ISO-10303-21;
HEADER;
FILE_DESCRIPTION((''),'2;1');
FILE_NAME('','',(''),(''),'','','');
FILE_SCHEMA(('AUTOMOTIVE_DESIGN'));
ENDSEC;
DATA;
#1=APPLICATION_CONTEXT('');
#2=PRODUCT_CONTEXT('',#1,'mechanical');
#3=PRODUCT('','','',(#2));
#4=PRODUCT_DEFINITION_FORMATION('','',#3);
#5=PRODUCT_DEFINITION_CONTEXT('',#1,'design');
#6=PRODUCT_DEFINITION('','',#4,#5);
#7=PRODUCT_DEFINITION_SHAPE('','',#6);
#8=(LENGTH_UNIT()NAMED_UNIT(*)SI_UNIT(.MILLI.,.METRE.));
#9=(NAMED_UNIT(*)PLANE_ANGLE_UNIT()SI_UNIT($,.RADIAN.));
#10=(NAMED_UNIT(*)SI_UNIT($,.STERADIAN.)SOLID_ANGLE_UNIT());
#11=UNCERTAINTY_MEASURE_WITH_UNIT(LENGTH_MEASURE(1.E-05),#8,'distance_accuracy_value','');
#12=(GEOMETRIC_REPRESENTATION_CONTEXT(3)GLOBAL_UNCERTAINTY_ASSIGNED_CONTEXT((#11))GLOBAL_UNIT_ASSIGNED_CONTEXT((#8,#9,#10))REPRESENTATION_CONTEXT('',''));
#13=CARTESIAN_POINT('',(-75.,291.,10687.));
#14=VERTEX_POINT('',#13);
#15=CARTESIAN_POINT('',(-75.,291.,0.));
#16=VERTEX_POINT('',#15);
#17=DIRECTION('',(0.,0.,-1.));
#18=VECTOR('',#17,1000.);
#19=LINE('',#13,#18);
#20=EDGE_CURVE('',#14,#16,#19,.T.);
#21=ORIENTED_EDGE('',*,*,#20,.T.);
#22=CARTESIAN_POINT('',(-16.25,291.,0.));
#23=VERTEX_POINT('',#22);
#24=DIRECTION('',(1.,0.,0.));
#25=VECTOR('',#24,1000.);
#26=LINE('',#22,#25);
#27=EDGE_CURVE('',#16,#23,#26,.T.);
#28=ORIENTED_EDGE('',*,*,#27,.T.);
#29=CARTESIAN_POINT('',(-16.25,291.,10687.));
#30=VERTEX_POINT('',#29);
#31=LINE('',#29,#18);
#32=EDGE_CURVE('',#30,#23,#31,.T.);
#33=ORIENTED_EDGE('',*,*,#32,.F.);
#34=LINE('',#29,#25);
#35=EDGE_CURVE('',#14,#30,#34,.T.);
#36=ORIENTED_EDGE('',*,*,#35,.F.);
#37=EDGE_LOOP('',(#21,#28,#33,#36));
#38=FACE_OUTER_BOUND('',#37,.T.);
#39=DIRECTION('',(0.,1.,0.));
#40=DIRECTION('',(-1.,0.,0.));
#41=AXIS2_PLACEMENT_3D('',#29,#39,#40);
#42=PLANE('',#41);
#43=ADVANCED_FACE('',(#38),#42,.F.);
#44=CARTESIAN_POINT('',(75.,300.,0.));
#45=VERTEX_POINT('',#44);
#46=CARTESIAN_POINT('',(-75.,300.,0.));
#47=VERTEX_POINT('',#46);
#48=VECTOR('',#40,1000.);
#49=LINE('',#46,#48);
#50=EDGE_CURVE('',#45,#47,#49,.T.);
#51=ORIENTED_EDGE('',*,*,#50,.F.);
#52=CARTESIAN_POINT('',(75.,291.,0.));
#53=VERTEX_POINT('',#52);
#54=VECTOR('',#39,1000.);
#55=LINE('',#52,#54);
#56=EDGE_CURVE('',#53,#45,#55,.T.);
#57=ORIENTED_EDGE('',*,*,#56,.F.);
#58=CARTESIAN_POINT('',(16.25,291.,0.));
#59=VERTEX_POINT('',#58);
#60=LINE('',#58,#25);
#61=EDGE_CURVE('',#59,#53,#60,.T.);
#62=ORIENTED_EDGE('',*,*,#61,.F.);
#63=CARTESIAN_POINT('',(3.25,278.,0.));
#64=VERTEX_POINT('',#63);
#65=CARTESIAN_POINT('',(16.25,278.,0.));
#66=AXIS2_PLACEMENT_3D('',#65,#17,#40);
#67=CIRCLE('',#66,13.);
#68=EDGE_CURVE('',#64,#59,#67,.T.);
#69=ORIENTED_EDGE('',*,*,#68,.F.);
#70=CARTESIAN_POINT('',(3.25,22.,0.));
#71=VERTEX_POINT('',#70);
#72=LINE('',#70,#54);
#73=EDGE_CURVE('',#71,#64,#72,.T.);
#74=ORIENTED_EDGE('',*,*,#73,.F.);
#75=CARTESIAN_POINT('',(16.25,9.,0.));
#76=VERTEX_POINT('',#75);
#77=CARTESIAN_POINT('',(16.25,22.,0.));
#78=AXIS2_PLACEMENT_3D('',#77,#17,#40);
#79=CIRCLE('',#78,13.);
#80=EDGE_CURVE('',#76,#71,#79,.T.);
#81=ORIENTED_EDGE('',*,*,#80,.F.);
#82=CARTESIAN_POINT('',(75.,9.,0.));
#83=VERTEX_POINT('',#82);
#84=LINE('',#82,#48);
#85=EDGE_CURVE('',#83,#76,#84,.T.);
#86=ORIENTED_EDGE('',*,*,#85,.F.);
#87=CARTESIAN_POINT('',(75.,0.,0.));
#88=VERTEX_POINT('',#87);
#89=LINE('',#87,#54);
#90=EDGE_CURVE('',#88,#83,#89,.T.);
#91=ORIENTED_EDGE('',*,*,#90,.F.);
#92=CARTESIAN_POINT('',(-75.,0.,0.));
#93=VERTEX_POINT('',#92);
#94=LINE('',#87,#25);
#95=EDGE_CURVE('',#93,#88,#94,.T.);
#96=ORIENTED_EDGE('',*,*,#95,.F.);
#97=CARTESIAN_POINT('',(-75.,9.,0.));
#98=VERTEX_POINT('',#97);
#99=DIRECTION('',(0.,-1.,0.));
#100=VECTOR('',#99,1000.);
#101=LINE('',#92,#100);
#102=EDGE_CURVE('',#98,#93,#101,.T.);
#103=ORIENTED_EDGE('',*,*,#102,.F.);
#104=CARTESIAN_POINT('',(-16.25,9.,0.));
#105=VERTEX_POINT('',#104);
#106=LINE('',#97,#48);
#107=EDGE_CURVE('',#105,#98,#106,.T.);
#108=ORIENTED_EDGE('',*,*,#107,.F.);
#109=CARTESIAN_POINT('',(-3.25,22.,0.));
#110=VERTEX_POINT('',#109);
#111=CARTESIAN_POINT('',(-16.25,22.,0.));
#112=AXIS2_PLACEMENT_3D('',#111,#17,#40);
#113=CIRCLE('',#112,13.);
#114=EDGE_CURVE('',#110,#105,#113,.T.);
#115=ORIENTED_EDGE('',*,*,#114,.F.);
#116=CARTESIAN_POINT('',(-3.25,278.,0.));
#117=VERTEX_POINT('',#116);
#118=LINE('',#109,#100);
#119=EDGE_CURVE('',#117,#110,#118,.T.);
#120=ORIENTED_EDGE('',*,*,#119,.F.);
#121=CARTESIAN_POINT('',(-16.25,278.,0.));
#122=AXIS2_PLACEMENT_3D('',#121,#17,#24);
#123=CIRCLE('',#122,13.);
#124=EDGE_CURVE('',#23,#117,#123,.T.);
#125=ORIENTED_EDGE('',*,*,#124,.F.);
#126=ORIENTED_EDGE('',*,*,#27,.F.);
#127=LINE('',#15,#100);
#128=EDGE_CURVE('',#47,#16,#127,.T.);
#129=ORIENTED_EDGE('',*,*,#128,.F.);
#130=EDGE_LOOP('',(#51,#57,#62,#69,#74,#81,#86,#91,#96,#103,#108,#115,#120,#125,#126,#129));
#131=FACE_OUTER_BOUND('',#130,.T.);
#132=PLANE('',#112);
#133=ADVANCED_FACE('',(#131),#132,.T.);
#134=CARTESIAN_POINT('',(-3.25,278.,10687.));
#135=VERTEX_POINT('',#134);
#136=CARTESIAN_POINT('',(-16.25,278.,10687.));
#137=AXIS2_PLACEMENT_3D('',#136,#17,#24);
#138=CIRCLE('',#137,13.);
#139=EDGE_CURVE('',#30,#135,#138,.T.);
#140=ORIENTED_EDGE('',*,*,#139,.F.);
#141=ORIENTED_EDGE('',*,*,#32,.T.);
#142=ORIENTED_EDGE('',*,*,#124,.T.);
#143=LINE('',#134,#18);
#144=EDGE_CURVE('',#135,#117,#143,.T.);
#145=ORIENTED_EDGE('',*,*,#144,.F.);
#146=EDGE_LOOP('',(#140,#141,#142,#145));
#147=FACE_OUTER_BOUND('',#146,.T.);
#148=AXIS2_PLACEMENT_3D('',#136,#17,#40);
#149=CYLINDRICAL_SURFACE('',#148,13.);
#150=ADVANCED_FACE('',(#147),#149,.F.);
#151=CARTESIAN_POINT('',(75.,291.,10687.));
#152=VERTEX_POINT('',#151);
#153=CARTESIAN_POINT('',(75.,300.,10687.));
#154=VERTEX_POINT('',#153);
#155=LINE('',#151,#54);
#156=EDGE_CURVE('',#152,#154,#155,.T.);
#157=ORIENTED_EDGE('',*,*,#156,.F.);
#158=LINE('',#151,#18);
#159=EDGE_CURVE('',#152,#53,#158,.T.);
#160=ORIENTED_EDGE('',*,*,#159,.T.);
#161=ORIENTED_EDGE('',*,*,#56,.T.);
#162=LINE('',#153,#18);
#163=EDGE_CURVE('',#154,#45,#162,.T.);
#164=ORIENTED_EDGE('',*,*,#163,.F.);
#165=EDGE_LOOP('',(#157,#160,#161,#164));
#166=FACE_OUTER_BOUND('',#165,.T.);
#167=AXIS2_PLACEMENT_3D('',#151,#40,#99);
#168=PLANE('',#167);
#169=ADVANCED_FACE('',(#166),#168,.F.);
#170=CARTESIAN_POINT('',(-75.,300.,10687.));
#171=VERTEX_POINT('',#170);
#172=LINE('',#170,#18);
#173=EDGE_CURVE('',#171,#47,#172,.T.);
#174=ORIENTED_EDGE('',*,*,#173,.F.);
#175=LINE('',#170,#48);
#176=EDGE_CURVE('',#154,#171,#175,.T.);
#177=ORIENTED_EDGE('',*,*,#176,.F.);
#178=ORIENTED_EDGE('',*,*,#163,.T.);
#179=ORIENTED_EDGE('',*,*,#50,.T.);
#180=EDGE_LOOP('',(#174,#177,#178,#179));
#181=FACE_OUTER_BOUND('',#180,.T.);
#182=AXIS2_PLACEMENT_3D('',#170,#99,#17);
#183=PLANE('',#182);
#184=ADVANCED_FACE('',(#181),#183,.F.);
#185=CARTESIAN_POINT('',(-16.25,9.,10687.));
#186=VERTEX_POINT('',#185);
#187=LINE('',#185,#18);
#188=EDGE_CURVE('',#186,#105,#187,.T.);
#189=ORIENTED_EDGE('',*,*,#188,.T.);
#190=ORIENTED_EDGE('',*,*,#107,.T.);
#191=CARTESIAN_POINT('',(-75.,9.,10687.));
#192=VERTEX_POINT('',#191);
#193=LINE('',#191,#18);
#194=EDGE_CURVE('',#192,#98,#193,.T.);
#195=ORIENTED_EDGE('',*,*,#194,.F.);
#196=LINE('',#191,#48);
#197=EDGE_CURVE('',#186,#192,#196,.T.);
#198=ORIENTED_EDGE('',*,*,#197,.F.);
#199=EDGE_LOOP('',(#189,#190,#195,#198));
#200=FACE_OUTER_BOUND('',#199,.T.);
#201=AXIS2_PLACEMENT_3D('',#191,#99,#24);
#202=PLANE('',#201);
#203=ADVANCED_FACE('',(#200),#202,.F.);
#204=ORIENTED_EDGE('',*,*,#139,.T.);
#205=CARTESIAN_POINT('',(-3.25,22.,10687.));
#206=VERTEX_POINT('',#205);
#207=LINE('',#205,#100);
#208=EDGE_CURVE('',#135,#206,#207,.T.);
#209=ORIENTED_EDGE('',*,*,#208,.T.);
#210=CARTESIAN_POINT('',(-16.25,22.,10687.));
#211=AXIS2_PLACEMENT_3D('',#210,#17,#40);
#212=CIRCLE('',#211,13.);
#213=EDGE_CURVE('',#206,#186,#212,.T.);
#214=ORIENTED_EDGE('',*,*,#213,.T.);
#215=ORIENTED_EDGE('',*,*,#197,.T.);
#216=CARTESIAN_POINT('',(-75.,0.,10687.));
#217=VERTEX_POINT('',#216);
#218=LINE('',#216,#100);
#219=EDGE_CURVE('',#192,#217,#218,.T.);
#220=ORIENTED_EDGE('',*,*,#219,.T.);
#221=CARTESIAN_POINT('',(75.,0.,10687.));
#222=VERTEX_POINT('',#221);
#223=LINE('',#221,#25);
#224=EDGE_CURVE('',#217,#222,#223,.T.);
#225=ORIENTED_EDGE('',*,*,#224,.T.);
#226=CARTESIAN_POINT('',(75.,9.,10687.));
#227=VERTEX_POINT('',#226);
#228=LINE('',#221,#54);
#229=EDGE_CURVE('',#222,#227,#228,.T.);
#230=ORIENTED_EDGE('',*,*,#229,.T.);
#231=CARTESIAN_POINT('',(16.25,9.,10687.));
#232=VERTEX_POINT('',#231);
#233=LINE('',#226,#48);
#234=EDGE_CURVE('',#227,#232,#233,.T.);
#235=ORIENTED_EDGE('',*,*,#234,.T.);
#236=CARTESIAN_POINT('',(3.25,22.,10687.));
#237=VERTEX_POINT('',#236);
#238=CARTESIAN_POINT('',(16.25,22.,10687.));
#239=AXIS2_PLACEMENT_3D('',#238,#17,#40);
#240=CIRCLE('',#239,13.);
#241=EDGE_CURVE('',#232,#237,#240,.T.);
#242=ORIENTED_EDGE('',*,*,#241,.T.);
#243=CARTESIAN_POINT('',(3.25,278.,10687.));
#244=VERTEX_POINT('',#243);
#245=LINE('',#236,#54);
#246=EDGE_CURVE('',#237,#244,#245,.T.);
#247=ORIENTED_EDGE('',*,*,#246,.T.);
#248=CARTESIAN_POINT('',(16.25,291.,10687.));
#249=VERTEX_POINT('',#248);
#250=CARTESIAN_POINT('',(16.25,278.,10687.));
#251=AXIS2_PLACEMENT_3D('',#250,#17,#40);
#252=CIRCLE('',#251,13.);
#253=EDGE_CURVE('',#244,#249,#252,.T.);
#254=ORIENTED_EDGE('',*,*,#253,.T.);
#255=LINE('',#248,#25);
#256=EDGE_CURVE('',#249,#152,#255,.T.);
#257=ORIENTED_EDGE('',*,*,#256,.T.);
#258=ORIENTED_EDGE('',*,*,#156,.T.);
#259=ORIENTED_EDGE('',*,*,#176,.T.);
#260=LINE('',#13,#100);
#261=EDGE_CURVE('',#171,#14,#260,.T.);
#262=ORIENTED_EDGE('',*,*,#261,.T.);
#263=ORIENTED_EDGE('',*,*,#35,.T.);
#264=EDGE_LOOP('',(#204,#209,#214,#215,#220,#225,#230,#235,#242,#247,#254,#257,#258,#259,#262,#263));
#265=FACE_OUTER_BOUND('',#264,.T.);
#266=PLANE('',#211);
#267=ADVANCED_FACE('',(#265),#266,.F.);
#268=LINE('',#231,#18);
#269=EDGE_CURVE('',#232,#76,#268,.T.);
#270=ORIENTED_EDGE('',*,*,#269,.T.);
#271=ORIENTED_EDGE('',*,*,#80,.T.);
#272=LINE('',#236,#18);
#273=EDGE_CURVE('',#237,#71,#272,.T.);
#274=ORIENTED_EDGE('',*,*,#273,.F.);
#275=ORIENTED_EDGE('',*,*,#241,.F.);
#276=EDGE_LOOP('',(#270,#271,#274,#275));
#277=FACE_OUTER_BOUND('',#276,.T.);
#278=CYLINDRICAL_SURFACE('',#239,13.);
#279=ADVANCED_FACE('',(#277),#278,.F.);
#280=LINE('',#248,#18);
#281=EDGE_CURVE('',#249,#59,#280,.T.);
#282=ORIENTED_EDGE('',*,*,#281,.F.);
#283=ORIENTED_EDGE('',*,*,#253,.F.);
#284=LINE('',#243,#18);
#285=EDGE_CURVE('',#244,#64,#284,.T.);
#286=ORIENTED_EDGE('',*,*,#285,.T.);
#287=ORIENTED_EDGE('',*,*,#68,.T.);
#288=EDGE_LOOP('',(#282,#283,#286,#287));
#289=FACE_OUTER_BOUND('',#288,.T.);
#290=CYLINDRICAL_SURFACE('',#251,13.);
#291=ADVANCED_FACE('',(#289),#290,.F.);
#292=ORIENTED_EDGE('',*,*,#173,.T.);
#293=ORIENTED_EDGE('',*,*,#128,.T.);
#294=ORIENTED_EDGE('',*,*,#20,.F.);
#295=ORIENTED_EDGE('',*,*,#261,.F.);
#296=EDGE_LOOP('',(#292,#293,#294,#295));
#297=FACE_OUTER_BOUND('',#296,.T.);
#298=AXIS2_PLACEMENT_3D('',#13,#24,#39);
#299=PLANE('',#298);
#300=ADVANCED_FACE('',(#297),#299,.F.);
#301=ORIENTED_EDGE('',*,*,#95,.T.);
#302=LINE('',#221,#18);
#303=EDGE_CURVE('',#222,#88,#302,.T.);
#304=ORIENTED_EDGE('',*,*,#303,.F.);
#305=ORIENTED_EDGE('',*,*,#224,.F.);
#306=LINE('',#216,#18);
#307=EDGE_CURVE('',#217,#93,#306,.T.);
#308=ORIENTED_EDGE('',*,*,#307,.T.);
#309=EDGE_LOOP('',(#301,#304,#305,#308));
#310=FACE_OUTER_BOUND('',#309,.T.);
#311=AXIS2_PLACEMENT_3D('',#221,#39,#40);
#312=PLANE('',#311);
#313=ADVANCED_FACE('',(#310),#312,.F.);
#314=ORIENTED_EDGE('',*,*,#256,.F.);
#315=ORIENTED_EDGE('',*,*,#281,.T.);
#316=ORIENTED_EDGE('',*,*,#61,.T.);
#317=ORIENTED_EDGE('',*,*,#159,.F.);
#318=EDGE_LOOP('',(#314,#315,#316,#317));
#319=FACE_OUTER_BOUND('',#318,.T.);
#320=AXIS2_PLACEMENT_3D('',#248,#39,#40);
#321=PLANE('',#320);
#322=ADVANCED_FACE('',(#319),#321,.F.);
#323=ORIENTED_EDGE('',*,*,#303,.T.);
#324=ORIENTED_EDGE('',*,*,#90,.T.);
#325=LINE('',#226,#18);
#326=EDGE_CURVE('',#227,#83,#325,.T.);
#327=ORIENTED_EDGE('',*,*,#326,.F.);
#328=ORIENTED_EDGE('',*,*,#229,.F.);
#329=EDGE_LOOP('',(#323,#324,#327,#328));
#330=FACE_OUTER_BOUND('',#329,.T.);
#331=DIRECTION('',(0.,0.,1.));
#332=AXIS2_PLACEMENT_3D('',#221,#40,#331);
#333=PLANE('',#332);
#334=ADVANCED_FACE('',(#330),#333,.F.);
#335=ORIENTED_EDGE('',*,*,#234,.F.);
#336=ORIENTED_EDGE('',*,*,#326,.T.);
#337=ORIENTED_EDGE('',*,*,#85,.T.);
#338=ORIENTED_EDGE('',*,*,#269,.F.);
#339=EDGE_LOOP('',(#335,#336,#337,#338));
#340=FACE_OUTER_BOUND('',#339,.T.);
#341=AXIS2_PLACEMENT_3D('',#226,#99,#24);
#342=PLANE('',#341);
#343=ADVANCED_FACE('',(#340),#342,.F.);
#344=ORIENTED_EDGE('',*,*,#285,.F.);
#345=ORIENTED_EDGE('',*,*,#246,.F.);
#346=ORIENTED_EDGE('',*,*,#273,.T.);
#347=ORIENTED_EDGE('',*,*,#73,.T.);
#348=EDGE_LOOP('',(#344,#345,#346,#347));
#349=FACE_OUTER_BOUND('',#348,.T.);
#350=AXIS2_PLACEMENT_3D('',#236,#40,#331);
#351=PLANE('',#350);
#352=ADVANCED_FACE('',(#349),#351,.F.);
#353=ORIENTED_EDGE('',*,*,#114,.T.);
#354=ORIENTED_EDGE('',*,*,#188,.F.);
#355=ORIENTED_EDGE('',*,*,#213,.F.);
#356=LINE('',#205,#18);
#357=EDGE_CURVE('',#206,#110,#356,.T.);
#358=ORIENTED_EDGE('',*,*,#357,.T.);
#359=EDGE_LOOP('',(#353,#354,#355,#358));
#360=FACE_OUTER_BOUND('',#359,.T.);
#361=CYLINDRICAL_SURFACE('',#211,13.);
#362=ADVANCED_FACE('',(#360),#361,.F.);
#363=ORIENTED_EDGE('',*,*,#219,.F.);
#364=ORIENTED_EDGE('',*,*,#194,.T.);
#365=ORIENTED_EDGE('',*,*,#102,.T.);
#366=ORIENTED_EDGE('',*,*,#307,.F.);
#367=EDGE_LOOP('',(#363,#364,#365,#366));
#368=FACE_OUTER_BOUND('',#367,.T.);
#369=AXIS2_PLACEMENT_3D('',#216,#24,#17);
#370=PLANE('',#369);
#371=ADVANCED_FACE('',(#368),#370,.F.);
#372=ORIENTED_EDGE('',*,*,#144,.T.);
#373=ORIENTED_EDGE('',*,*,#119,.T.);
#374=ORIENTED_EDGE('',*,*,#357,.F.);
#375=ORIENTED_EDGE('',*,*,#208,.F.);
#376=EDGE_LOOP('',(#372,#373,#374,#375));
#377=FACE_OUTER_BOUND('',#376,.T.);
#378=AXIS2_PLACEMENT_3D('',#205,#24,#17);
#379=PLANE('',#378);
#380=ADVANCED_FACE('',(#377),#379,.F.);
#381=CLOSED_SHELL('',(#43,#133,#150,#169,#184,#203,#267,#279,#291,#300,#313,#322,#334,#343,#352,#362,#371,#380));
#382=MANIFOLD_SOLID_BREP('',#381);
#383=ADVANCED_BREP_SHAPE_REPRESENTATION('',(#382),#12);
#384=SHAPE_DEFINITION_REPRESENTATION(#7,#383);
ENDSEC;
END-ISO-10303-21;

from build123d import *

# Parameters (mm, degrees)
BOSS_EXTRUDE1_DEPTH = 10687


with BuildPart() as part:
    # Sketch1 → Boss-Extrude1 (new body)
    with BuildSketch(Plane.XY):
        with BuildLine():
            Line((75, 0), (-75, 0))
            Line((-75, 0), (-75, 9))
            Line((-75, 9), (-16.25, 9))
            ThreePointArc((-16.25, 9), (-7.057611845, 12.807611845), (-3.25, 22))
            Line((-3.25, 22), (-3.25, 278))
            ThreePointArc((-3.25, 278), (-7.057611845, 287.192388155), (-16.25, 291))
            Line((-16.25, 291), (-75, 291))
            Line((-75, 291), (-75, 300))
            Line((-75, 300), (75, 300))
            Line((75, 300), (75, 291))
            Line((75, 291), (16.25, 291))
            ThreePointArc((16.25, 291), (7.057611845, 287.192388155), (3.25, 278))
            Line((3.25, 278), (3.25, 22))
            ThreePointArc((3.25, 22), (7.057611845, 12.807611845), (16.25, 9))
            Line((16.25, 9), (75, 9))
            Line((75, 9), (75, 0))
        make_face()
    extrude(amount=BOSS_EXTRUDE1_DEPTH)


solid = part.part
